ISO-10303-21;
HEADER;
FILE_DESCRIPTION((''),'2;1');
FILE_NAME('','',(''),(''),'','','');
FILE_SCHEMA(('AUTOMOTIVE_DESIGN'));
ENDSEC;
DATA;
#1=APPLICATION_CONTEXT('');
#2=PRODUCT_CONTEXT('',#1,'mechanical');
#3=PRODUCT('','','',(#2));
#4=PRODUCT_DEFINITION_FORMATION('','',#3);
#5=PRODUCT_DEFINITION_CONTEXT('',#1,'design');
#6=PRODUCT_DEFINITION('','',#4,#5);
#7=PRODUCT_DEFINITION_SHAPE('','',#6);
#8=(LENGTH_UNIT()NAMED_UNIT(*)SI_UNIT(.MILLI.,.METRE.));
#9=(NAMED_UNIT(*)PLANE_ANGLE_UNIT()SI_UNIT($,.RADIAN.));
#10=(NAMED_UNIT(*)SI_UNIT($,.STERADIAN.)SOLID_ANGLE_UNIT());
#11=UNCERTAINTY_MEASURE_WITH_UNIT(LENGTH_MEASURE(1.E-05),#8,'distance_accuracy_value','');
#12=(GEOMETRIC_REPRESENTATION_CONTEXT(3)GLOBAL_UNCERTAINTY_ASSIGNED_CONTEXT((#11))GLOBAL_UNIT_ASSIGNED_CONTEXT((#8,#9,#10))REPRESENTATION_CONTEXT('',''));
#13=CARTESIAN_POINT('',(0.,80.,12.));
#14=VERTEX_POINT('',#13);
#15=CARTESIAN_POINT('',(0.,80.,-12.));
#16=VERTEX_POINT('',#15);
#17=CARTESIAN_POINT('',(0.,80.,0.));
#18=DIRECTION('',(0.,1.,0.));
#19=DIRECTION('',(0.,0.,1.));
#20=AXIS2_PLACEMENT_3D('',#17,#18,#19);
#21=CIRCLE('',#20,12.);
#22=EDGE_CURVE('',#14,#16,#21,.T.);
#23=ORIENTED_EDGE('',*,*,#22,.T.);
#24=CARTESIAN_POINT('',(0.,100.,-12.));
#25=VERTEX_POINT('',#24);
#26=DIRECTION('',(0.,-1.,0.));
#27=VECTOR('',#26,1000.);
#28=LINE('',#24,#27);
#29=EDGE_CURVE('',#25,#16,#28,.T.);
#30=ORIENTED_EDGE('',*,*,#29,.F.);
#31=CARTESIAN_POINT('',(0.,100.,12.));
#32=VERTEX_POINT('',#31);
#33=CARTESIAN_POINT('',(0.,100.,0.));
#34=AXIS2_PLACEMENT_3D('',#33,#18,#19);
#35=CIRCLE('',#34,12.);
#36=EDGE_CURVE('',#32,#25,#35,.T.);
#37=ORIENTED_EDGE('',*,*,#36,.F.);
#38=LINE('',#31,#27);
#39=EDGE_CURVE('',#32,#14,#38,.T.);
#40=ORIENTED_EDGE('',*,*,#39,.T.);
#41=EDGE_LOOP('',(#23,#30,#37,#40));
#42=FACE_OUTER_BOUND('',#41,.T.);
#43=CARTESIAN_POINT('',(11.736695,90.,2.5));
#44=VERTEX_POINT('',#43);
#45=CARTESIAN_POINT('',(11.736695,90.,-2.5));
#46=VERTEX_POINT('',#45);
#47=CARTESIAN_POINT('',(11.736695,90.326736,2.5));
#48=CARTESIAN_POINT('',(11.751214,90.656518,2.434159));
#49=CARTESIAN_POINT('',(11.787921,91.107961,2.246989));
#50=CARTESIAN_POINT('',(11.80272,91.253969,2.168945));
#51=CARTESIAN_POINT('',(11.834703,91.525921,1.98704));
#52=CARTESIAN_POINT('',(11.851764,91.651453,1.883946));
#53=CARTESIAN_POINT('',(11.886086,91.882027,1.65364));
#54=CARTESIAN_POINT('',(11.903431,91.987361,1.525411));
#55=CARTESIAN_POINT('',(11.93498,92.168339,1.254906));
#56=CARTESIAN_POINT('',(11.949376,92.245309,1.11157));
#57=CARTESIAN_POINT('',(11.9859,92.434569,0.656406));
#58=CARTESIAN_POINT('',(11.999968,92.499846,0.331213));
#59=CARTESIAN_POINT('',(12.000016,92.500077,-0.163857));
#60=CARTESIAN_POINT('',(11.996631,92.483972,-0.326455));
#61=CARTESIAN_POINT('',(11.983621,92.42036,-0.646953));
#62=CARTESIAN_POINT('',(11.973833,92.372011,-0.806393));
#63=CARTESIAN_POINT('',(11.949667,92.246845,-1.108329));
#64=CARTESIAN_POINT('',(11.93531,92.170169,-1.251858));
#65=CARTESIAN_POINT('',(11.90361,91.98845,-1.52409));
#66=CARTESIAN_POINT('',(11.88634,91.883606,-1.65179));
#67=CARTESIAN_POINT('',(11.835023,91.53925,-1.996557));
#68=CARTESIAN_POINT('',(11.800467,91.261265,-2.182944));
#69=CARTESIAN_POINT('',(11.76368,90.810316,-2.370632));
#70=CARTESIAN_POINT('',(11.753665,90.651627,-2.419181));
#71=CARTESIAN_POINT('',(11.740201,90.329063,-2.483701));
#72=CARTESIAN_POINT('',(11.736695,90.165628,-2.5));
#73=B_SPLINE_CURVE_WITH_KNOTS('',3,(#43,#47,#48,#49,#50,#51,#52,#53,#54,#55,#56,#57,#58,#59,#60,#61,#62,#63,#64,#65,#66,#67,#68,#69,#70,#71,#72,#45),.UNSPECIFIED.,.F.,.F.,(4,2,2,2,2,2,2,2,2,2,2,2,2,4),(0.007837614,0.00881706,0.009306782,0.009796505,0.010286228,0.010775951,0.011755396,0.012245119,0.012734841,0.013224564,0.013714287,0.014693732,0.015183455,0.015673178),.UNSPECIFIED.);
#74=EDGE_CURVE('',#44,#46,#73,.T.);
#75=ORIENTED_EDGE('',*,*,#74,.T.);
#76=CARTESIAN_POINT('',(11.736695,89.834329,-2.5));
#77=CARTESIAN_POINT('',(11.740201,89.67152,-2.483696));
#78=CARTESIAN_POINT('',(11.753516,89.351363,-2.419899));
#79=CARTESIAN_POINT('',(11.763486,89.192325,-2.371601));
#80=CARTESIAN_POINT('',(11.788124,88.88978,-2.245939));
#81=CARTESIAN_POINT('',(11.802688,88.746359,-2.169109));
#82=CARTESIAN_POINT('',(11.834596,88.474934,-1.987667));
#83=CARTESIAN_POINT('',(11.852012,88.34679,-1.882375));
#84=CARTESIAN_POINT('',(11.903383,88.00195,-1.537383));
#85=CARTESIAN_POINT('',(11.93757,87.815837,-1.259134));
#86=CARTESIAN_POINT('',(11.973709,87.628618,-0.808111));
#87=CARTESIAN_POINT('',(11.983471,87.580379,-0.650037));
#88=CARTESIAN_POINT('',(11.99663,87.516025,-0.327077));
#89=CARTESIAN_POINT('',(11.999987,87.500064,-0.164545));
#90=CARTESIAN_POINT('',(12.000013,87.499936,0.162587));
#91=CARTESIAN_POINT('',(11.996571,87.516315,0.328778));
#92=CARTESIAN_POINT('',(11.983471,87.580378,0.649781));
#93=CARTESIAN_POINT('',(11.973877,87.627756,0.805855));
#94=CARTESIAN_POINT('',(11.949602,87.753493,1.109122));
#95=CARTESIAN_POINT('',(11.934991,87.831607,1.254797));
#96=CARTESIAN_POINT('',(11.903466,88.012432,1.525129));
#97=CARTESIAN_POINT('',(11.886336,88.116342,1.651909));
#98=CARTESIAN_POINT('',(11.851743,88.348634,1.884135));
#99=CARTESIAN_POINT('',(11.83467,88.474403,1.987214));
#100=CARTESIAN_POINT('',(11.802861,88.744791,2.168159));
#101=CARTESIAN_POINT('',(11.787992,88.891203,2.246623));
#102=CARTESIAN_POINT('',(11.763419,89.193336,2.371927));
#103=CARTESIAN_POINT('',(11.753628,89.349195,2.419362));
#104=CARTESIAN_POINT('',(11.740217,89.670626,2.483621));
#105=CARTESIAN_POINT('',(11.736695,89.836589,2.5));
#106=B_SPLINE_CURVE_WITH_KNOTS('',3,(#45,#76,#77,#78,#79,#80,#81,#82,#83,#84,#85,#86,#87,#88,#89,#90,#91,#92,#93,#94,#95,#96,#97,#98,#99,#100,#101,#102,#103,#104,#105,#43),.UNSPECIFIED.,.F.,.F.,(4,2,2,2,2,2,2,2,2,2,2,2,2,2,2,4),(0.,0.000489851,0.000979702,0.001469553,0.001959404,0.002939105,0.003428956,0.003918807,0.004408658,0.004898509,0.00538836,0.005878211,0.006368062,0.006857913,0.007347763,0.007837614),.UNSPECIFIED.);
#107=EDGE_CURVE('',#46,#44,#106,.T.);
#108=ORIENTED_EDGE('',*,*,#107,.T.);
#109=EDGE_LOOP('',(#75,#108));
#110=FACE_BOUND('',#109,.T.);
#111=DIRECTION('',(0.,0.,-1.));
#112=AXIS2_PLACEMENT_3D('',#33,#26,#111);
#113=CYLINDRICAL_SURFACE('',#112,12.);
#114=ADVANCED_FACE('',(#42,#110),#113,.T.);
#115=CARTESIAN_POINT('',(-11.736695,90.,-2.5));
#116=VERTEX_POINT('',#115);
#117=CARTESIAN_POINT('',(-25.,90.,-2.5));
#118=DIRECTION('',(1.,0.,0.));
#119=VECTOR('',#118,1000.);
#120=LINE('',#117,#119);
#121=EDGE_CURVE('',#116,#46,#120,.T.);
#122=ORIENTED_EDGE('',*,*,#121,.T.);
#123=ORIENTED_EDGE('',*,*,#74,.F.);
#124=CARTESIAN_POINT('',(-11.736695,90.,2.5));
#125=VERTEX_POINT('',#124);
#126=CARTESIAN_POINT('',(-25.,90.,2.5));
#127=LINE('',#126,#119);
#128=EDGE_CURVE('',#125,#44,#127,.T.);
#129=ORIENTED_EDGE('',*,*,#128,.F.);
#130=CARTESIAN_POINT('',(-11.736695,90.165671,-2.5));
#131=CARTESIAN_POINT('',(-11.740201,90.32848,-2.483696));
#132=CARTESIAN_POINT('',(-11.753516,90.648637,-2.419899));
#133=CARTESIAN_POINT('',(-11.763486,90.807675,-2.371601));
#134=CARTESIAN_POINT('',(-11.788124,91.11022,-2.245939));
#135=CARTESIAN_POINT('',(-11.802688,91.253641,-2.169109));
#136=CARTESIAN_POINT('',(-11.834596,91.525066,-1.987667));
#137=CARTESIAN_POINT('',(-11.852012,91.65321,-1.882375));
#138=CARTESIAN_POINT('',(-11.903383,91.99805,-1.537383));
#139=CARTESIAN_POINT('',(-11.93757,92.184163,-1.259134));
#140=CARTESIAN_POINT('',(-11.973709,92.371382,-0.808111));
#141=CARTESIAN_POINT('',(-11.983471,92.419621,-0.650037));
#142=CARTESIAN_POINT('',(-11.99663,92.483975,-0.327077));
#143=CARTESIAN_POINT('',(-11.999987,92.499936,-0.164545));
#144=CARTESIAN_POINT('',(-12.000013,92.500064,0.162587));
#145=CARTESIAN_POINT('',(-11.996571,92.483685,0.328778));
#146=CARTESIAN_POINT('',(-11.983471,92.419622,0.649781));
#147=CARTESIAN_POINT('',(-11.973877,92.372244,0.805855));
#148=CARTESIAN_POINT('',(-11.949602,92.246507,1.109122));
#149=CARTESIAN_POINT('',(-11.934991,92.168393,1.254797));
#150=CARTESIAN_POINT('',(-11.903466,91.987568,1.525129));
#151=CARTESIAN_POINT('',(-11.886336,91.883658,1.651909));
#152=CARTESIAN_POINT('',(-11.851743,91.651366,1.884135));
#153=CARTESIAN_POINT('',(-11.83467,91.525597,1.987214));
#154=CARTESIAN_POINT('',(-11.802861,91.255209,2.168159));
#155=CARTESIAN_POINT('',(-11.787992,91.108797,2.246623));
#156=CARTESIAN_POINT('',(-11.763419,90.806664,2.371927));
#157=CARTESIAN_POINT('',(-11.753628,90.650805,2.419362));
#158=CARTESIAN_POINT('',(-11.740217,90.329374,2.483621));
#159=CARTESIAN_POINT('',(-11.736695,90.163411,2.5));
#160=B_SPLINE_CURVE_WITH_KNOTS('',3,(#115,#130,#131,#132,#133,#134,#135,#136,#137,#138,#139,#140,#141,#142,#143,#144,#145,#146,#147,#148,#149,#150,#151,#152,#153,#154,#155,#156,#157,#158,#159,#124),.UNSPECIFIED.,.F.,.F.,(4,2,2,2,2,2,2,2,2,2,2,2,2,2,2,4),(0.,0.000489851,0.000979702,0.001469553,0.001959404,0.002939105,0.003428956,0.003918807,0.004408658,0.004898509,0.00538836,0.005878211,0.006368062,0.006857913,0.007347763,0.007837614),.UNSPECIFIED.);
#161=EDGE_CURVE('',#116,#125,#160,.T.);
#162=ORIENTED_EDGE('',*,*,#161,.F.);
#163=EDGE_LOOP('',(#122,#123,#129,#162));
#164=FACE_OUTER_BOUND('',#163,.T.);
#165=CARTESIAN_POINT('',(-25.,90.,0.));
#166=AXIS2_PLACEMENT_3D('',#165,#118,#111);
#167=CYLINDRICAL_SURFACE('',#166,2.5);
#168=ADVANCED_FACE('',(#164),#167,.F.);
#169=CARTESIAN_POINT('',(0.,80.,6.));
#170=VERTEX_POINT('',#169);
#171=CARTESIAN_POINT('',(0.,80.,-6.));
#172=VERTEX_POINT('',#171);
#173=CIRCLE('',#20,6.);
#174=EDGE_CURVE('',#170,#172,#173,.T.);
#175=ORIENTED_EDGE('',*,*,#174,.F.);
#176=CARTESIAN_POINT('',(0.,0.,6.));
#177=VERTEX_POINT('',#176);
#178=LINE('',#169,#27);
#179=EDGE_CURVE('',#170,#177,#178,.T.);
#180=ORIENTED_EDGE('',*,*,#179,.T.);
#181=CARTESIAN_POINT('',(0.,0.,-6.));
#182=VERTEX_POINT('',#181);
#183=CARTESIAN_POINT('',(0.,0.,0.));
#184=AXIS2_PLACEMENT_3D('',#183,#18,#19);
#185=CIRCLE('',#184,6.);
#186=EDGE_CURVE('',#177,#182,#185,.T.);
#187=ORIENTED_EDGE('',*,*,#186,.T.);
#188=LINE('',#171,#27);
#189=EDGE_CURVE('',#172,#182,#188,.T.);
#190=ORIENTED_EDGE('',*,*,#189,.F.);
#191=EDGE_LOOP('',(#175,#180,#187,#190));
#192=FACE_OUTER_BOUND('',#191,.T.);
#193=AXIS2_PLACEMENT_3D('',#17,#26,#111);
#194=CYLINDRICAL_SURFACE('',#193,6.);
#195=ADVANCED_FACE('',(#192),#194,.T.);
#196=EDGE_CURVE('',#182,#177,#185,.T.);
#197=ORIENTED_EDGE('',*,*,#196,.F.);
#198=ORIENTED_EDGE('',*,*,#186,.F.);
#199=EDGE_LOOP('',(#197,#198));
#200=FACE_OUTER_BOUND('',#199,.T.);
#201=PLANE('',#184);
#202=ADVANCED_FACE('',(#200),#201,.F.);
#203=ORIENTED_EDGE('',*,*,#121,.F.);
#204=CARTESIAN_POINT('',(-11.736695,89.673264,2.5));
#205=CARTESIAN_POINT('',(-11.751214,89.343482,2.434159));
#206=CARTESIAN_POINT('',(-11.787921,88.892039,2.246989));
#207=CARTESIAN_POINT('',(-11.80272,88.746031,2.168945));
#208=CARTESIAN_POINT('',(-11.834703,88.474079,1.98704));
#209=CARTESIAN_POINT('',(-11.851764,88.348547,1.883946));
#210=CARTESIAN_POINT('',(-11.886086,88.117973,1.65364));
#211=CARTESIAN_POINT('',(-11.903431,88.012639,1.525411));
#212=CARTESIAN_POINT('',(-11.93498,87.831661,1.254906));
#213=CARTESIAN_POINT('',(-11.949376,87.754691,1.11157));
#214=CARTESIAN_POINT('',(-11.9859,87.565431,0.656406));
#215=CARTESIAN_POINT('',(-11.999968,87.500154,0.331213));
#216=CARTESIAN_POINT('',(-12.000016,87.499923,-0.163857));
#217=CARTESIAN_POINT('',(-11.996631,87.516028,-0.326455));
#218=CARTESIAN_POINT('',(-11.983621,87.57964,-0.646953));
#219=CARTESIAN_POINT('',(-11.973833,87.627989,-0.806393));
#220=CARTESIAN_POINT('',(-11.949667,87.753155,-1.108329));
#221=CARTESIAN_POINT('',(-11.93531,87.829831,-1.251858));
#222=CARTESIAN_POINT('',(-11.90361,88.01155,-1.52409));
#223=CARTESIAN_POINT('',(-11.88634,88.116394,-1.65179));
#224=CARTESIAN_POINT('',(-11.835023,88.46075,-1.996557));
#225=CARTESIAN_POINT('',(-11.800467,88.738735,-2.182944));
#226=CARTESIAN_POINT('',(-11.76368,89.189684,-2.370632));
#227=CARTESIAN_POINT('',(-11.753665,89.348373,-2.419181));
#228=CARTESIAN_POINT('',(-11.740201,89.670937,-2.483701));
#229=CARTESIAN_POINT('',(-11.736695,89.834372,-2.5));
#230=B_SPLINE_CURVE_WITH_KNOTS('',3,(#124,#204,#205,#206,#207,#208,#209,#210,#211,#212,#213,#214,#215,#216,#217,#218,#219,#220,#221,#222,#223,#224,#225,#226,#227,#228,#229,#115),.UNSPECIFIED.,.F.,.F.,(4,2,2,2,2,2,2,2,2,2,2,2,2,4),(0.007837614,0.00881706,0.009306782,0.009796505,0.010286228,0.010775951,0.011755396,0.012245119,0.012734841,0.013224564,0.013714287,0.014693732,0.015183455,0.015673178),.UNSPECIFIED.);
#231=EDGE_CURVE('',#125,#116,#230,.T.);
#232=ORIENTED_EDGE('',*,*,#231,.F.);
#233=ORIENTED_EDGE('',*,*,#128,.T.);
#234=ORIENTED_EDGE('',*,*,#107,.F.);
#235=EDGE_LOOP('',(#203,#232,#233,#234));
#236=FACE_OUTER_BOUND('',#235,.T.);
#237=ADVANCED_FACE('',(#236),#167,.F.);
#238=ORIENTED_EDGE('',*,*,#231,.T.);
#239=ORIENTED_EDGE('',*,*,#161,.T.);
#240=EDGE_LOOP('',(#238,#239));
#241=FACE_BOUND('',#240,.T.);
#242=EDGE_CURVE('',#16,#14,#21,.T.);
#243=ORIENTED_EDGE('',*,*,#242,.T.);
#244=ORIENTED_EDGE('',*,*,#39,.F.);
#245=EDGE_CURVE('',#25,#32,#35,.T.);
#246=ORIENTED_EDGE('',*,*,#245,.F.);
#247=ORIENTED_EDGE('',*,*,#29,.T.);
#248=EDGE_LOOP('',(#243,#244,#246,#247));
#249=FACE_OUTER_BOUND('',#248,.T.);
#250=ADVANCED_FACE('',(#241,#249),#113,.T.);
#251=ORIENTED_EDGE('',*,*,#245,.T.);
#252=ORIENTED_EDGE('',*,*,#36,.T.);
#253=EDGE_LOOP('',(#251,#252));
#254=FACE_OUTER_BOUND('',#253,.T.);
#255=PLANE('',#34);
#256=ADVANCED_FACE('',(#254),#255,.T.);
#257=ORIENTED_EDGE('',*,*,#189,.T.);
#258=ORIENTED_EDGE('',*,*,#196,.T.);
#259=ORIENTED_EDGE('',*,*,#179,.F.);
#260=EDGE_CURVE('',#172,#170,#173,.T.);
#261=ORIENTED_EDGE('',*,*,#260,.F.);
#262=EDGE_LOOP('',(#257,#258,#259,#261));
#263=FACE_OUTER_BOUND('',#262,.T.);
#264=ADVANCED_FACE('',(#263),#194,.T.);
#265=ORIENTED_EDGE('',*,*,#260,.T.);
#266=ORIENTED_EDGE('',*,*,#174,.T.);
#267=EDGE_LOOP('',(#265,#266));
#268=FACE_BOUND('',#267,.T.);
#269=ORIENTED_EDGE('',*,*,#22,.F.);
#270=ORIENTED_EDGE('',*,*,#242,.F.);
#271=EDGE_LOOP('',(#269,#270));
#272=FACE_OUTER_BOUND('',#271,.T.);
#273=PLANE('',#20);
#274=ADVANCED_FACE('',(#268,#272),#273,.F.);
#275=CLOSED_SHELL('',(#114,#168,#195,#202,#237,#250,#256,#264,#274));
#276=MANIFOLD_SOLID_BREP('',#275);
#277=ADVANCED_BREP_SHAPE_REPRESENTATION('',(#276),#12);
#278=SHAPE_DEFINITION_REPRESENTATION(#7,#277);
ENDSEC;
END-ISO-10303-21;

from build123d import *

# Parameters (mm, degrees)
SHAFT_PROFILE_R      = 6
SHAFT_L80_DEPTH      = 80
HEAD_PROFILE_R       = 12
HEAD_24_X_20_DEPTH   = 20
CROSS_HOLE_PROFILE_R = 2.5
CROSS_HOLE_DEPTH     = 25


with BuildPart() as part:
    # Shaft Profile → Shaft L80 (new body)
    with BuildSketch(Plane(origin=(0, 0, 0), x_dir=(1, 0, 0), z_dir=(0, 1, 0))):
        with Locations(Location((0, 0, 0), (0, 0, 270))):
            Circle(SHAFT_PROFILE_R)
    extrude(amount=SHAFT_L80_DEPTH)

    # Head Profile → Head Ø24 x 20 (add)
    with BuildSketch(Plane(origin=(0, 80, 0), x_dir=(1, 0, 0), z_dir=(0, 1, 0))):
        with Locations(Location((0, 0, 0), (0, 0, 270))):
            Circle(HEAD_PROFILE_R)
    extrude(amount=HEAD_24_X_20_DEPTH)

    # Cross Hole Profile → Cross Hole (cut, symmetric)
    with BuildSketch(Plane(origin=(0, 0, 0), x_dir=(0, 0, -1), z_dir=(1, 0, 0))):
        with Locations((0, 90)):
            Circle(CROSS_HOLE_PROFILE_R)
    extrude(amount=CROSS_HOLE_DEPTH, both=True, mode=Mode.SUBTRACT)


solid = part.part
